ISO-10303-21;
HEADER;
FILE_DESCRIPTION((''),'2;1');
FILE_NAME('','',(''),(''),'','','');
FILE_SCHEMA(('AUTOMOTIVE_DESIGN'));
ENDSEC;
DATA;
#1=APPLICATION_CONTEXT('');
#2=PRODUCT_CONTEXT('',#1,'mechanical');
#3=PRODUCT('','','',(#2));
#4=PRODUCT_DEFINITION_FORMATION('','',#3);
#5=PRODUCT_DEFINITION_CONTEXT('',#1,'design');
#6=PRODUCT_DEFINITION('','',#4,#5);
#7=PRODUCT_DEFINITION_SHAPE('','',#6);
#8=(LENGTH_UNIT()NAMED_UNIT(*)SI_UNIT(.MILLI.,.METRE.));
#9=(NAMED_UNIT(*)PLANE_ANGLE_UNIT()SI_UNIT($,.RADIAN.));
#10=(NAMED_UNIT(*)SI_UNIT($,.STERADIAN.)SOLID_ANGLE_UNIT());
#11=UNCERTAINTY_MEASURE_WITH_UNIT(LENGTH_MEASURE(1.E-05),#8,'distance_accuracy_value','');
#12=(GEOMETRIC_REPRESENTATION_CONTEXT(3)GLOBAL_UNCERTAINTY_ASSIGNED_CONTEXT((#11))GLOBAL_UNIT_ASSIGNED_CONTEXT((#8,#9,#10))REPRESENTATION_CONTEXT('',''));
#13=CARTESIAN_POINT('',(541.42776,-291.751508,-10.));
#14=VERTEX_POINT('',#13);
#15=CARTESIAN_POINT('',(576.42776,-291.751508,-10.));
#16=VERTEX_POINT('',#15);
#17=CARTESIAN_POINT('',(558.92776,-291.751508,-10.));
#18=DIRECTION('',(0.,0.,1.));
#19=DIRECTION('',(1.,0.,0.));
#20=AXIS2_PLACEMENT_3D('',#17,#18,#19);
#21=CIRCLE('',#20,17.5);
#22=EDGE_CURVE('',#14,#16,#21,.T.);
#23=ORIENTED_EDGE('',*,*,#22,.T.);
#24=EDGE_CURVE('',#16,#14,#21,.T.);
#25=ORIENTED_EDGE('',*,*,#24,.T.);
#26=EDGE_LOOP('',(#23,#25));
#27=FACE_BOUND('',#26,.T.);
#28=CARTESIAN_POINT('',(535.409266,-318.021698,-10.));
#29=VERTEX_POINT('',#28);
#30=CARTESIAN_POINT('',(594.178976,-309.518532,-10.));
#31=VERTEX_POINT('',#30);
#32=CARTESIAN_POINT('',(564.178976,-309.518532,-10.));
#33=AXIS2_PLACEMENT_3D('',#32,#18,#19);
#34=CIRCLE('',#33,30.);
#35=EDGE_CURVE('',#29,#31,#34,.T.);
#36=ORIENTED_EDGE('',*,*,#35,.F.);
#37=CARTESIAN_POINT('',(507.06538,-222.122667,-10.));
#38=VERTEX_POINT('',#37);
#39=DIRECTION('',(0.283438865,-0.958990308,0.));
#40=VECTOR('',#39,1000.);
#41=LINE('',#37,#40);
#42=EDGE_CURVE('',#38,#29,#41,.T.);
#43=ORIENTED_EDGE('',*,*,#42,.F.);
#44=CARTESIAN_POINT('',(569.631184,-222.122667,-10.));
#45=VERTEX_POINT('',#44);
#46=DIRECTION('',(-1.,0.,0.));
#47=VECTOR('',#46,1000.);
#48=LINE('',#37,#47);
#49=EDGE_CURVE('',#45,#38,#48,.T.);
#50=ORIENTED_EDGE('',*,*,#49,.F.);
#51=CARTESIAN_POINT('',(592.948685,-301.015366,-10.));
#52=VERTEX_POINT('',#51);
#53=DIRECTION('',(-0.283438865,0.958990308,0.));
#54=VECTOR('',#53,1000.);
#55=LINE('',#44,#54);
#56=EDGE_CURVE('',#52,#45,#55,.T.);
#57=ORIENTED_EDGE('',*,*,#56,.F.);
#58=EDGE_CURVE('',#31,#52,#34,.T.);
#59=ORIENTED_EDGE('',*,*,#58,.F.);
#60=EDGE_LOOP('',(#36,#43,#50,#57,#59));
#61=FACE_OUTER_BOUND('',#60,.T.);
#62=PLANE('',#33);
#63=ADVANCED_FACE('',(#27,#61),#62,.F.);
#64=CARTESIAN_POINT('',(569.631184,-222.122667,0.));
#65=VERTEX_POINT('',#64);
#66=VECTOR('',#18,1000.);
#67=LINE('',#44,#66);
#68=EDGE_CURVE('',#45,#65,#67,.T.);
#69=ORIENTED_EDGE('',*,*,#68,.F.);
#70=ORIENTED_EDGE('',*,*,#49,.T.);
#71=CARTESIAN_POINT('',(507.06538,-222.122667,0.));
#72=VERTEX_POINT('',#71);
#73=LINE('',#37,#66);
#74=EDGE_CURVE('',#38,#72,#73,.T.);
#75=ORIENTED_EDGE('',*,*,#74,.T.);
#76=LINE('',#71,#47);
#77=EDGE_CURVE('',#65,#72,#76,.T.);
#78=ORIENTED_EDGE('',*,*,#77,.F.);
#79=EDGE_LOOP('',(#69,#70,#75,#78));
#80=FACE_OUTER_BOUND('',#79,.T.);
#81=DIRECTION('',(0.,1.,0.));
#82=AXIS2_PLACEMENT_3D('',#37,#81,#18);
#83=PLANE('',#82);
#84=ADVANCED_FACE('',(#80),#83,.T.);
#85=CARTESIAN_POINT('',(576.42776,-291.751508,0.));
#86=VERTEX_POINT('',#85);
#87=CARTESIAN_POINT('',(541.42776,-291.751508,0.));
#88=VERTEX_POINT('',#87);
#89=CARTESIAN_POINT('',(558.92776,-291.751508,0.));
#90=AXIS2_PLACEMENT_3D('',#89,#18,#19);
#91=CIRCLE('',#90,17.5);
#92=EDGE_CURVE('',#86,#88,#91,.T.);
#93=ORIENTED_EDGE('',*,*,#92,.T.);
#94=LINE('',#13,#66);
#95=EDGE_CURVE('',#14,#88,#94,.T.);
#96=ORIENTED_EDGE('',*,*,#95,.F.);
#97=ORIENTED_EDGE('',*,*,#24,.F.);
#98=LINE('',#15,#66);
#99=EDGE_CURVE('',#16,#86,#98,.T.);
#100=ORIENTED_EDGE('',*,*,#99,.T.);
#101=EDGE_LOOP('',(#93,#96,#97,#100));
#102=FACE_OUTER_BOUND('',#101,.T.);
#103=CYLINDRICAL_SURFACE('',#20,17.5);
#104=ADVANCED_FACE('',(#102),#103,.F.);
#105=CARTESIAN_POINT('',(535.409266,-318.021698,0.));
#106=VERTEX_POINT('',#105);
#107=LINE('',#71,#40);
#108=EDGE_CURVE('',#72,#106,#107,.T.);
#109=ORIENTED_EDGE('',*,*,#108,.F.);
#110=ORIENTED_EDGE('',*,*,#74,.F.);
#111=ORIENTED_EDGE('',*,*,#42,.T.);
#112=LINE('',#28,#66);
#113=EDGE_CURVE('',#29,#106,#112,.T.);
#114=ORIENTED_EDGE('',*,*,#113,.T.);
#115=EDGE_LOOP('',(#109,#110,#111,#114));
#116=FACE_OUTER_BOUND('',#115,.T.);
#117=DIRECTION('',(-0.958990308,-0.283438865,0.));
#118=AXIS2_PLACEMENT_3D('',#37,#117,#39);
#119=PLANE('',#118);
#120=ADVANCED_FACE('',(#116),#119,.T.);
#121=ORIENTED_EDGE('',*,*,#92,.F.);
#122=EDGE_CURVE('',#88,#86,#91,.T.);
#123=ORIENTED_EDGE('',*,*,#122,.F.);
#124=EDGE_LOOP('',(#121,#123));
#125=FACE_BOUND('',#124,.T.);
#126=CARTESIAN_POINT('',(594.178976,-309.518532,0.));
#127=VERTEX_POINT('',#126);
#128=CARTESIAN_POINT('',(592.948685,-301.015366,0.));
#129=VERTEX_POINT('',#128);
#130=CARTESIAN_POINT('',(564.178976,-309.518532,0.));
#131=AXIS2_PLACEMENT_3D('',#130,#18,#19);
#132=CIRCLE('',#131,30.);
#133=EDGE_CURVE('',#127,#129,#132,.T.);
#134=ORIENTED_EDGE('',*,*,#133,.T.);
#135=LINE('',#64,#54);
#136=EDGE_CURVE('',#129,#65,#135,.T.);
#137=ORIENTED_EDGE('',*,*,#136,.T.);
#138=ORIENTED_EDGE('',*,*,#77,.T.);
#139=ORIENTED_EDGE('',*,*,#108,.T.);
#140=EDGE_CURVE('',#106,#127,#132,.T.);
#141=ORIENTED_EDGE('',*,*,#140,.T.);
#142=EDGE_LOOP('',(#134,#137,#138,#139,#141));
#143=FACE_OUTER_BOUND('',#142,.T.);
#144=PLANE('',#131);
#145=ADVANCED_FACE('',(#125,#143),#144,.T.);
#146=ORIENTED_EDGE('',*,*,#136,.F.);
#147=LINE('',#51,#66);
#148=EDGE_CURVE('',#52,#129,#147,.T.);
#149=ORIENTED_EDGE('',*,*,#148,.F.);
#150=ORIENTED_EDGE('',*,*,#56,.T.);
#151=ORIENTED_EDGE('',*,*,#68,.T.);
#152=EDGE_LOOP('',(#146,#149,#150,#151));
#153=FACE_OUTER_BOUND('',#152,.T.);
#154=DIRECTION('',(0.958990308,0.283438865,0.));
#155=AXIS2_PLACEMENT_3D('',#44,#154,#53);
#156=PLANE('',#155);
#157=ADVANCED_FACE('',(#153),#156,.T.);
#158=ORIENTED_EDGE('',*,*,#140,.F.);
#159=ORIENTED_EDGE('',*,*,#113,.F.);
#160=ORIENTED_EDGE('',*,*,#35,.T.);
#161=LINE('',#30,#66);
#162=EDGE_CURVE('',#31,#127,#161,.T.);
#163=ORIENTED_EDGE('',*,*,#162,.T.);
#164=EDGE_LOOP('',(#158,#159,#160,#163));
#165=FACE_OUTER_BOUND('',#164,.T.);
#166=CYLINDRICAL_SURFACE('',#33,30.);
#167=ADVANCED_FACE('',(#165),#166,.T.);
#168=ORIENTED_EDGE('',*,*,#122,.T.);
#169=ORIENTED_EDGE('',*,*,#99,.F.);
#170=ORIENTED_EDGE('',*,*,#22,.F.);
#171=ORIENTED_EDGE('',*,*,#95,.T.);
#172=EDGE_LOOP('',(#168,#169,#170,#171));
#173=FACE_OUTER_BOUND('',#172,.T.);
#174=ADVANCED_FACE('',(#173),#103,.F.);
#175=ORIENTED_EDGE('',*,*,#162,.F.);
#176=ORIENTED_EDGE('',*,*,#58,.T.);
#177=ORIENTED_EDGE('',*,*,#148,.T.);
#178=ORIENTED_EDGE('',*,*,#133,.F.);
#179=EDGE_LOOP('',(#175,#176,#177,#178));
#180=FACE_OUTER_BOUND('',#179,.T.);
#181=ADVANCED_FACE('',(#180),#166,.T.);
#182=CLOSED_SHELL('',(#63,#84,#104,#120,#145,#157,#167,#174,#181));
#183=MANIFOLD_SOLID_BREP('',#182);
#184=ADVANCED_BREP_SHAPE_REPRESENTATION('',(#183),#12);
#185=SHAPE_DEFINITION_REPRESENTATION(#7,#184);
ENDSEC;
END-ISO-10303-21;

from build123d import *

# Parameters (mm, degrees)
SKETCH_2_R      = 17.5
EXTRUDE_1_DEPTH = 10


with BuildPart() as part:
    # 草图2 → 凸台-拉伸1 (new body)
    with BuildSketch(Plane.XY):
        with BuildLine():
            Line((507.065379812, -222.122666991), (535.409266278, -318.021697747))
            ThreePointArc((535.409266278, -318.021697747), (572.682141445, -338.288241034), (592.948684732, -301.015365867))
            Line((592.948684732, -301.015365867), (569.631184207, -222.122666991))
            Line((569.631184207, -222.122666991), (507.065379812, -222.122666991))
        make_face()
        with Locations((558.927759659, -291.75150785)):
            Circle(SKETCH_2_R, mode=Mode.SUBTRACT)
    extrude(amount=-EXTRUDE_1_DEPTH)


solid = part.part
